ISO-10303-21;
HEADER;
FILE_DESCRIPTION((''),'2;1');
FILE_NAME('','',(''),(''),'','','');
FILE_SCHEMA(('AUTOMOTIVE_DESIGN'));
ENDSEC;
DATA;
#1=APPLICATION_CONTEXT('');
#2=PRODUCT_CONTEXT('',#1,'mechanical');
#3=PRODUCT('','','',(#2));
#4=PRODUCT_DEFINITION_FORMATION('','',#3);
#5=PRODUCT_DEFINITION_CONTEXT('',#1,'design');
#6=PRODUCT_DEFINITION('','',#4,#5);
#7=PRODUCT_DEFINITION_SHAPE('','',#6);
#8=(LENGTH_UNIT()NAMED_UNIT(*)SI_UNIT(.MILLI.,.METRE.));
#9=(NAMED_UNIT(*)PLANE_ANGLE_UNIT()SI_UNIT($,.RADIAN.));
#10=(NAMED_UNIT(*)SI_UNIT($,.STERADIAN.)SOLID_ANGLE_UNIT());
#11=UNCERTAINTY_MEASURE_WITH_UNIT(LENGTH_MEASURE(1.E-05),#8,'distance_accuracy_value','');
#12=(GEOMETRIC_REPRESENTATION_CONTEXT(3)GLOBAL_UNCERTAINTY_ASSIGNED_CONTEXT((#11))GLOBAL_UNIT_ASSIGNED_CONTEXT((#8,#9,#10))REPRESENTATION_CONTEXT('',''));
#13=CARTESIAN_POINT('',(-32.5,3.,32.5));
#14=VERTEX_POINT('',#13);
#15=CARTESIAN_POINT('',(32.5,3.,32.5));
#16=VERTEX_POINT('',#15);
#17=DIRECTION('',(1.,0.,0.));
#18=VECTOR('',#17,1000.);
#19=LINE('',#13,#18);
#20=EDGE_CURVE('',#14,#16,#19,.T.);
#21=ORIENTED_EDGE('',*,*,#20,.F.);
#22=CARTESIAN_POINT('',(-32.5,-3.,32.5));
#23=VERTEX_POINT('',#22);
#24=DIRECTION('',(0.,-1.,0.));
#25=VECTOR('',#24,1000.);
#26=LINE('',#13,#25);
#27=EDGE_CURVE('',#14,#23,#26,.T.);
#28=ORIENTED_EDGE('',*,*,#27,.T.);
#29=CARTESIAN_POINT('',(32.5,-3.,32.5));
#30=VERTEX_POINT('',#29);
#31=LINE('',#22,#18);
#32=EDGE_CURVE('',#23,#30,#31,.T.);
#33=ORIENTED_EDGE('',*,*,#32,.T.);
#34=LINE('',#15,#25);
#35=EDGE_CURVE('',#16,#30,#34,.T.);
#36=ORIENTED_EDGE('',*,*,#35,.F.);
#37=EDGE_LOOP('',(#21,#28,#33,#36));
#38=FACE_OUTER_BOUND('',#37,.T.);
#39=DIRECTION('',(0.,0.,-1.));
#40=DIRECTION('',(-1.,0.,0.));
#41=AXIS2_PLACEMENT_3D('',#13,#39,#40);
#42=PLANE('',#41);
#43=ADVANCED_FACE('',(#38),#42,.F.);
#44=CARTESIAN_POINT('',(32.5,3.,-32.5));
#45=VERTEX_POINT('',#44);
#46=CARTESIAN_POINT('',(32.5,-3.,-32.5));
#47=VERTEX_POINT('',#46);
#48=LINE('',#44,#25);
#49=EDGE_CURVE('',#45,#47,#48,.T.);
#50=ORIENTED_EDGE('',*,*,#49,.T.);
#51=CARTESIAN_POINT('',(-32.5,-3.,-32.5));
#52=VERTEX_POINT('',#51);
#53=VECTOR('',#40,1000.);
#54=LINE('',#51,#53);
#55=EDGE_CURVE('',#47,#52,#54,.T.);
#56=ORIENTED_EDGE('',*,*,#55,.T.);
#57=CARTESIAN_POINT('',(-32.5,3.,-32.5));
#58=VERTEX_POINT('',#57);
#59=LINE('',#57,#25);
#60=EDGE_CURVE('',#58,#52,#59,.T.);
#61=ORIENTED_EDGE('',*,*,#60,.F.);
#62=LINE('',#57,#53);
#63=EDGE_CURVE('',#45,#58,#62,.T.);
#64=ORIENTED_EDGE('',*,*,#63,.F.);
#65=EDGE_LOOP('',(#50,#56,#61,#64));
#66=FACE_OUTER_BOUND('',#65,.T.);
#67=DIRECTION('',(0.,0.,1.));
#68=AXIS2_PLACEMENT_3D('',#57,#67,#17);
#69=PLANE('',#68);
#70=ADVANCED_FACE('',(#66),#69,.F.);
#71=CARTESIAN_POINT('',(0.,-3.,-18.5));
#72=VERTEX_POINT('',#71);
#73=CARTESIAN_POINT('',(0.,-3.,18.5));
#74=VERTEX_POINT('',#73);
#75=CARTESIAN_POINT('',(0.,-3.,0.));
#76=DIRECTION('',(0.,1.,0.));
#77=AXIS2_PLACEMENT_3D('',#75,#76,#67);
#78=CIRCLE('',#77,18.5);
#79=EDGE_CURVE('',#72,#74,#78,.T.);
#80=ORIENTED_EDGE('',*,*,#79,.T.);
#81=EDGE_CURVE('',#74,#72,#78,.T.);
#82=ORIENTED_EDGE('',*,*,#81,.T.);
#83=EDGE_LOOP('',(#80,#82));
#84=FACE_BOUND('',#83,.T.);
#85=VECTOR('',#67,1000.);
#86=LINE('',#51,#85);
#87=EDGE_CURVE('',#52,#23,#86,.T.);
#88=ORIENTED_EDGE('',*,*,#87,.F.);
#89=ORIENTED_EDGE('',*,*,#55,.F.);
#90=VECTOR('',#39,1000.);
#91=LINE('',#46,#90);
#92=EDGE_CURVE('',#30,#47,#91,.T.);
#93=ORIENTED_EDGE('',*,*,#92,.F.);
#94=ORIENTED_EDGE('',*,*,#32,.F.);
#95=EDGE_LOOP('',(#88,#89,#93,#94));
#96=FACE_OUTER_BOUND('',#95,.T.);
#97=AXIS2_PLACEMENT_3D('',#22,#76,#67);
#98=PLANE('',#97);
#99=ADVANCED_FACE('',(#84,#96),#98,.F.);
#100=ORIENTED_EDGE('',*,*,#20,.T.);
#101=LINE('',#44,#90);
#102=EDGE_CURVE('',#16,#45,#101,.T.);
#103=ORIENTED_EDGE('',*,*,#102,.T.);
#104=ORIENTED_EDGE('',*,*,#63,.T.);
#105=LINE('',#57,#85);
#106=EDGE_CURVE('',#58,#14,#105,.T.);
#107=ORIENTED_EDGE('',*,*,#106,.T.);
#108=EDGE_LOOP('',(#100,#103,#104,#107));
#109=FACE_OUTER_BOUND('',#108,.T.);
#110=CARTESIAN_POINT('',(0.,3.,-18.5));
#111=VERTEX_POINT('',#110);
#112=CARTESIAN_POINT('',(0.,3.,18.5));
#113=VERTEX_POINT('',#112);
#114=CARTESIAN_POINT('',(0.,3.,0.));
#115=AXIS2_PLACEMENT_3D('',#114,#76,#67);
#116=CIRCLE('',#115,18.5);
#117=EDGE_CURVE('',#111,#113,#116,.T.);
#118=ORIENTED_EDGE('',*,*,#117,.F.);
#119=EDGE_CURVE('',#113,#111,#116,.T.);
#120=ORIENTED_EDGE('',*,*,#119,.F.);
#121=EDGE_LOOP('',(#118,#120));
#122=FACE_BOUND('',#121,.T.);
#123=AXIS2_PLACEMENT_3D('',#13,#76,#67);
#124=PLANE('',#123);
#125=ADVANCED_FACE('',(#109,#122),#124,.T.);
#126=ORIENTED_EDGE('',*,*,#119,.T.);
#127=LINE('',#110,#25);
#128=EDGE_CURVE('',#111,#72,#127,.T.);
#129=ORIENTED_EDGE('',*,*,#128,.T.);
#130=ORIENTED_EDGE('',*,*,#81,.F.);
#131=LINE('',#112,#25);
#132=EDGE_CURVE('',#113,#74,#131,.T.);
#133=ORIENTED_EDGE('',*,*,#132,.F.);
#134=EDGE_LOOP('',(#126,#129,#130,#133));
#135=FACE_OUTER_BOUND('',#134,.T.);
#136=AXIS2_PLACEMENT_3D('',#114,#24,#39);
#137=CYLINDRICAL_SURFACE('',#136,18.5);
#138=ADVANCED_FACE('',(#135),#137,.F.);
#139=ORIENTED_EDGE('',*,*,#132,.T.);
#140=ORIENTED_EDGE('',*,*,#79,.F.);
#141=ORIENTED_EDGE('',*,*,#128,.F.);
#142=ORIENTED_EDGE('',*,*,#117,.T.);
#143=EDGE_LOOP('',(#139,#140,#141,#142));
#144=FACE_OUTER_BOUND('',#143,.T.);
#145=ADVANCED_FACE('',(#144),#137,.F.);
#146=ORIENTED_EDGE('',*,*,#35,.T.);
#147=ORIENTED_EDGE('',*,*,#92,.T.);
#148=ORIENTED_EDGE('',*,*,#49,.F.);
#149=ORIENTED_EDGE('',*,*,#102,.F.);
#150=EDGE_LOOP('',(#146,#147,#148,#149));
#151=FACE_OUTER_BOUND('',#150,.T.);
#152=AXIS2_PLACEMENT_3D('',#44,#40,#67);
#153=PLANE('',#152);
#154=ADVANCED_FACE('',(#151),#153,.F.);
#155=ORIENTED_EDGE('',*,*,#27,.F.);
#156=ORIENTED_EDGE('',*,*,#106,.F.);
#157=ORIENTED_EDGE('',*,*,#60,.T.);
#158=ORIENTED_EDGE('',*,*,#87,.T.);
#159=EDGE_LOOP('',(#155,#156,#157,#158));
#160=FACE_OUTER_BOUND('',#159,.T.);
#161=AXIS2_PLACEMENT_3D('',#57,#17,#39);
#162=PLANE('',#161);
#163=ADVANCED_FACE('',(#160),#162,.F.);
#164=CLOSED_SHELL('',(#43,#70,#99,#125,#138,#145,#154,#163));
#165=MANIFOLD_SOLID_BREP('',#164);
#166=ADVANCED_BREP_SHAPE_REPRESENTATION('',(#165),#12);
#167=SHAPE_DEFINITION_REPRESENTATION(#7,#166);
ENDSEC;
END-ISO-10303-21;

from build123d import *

# Parameters (mm, degrees)
SKETCH2_W           = 65
SKETCH2_H           = 65
SKETCH2_R           = 18.5
BOSS_EXTRUDE1_DEPTH = 3


with BuildPart() as part:
    # Sketch2 → Boss-Extrude1 (new, symmetric)
    with BuildSketch(Plane(origin=(0, 0, 0), x_dir=(1, 0, 0), z_dir=(0, 1, 0))):
        Rectangle(SKETCH2_W, SKETCH2_H)
        with Locations(Location((0, 0, 0), (0, 0, 270))):
            Circle(SKETCH2_R, mode=Mode.SUBTRACT)
    extrude(amount=BOSS_EXTRUDE1_DEPTH, both=True)


solid = part.part
